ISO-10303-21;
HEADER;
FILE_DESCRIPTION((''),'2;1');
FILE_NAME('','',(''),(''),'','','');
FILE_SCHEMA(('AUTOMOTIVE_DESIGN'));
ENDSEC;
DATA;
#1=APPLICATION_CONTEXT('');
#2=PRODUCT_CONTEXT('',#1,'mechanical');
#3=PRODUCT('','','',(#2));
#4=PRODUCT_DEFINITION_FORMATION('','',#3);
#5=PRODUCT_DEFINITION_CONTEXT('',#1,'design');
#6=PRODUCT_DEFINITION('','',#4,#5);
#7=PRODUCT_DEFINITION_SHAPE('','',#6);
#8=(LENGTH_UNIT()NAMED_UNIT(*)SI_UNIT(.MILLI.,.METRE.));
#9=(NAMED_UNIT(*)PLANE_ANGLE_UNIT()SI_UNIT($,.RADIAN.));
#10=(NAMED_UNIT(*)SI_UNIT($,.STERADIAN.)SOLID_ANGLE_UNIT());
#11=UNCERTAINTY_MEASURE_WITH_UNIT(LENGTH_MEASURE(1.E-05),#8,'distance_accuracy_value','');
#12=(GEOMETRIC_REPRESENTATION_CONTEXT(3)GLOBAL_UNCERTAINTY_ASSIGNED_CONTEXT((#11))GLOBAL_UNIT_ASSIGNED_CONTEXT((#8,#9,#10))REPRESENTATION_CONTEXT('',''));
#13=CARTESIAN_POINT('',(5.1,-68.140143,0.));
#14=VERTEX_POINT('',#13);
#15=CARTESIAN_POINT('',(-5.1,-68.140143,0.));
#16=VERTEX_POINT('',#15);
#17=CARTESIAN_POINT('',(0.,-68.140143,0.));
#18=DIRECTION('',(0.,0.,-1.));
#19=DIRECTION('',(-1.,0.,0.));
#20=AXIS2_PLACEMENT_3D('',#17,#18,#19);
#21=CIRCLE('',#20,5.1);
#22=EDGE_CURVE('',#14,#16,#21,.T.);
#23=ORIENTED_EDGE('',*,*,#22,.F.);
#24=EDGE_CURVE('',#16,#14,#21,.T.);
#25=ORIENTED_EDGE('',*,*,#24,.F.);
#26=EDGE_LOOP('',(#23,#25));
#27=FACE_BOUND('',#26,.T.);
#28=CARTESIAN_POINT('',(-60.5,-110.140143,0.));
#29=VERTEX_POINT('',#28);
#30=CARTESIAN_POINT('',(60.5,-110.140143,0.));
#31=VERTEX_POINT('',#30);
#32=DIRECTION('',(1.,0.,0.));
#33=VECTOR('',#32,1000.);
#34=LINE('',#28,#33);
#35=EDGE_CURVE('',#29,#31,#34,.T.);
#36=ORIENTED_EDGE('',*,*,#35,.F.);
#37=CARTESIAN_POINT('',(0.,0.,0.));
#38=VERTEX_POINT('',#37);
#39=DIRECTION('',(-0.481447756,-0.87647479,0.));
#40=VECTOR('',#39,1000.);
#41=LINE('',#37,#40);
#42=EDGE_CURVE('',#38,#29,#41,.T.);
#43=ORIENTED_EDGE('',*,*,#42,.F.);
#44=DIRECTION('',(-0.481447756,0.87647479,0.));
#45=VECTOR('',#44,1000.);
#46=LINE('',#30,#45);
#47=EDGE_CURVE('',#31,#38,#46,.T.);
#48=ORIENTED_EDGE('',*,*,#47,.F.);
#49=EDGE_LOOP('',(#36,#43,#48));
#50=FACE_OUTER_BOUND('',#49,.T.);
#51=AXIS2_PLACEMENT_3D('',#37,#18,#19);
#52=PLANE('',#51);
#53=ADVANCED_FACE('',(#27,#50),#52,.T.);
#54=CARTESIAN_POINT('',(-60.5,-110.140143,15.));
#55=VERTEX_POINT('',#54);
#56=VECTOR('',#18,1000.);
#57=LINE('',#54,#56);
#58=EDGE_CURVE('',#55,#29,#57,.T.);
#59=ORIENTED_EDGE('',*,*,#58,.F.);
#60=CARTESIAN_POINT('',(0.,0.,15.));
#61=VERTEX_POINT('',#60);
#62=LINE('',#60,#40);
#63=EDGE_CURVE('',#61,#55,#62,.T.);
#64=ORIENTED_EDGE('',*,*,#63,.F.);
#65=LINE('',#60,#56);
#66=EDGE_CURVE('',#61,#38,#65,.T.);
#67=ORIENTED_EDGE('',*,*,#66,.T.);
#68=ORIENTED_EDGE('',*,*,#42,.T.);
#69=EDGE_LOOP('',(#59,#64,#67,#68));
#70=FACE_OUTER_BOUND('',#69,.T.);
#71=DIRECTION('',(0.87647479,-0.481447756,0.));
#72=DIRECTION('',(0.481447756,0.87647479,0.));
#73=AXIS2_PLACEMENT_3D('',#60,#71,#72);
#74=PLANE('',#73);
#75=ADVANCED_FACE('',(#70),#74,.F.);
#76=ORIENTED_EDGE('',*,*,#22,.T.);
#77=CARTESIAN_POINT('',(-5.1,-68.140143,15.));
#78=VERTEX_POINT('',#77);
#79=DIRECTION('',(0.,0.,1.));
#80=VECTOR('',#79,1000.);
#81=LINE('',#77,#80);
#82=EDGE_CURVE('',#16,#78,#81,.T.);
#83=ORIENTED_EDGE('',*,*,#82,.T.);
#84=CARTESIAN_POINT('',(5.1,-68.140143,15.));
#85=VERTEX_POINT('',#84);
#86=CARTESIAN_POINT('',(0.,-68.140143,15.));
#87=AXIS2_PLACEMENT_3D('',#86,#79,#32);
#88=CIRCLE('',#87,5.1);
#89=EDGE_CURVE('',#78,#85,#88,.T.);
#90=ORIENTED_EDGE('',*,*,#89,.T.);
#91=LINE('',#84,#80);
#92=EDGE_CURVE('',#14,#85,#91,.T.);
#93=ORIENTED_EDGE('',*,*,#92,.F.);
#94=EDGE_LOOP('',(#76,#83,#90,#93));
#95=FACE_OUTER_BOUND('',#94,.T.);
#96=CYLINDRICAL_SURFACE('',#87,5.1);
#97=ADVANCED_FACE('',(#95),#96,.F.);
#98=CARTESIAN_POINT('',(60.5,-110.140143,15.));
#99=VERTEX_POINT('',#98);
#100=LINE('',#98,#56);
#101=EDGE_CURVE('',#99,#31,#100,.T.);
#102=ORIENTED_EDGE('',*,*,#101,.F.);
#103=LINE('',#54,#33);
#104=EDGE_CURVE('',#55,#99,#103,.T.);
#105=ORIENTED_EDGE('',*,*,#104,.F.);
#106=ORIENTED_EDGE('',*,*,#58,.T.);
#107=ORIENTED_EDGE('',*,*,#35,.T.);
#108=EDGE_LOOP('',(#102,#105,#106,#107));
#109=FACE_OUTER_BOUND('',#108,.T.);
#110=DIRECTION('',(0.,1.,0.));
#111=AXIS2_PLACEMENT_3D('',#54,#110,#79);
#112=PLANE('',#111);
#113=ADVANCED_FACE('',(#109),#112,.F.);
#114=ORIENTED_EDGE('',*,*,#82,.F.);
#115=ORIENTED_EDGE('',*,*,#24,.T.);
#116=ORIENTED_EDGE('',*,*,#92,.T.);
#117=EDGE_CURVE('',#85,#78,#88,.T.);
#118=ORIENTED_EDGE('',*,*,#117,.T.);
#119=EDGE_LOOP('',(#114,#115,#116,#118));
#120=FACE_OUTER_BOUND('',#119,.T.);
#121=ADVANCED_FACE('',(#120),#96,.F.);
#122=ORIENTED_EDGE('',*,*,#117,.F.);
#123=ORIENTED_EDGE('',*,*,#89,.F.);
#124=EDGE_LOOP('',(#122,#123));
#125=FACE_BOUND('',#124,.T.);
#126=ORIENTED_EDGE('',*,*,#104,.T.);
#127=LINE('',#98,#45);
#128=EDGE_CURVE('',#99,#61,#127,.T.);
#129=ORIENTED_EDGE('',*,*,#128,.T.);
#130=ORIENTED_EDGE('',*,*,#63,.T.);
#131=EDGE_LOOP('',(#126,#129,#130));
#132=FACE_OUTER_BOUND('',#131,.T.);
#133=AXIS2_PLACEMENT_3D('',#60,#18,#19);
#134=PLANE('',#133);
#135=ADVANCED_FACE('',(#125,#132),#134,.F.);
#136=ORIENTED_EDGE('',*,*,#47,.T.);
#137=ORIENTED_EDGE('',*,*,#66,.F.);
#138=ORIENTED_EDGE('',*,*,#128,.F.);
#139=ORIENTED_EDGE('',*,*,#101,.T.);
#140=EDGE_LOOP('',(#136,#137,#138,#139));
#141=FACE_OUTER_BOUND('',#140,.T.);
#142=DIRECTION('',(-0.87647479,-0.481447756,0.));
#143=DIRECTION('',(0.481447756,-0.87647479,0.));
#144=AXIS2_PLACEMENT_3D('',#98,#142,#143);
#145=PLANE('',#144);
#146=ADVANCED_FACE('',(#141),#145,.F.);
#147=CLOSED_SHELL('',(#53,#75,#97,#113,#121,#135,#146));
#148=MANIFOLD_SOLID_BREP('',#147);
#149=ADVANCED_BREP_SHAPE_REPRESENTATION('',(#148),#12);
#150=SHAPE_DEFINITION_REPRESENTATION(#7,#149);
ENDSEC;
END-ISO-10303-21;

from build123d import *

# Parameters (mm, degrees)
SKETCH1_R              = 4.5
BOSS_EXTRUDE1_DEPTH    = 15
M12_TAPPED_HOLE1_D     = 10.2
M12_TAPPED_HOLE1_DEPTH = 29.25
M12_TAPPED_HOLE1_TIP   = 3.064389157


with BuildPart() as part:
    # Sketch1 → Boss-Extrude1 (new body)
    with BuildSketch(Plane.XY):
        Polygon((0, 0), (-60.5, -110.140143259), (60.5, -110.140143259), align=None)
        with Locations((0, -68.140143259)):
            Circle(SKETCH1_R, mode=Mode.SUBTRACT)
    extrude(amount=BOSS_EXTRUDE1_DEPTH)

    # M12 Tapped Hole1
    with Locations(Plane.XY.offset(15)):
        with Locations((0, -68.140143259)):
            Hole(M12_TAPPED_HOLE1_D / 2, depth=M12_TAPPED_HOLE1_DEPTH)
            with Locations((0, 0, -(M12_TAPPED_HOLE1_DEPTH + M12_TAPPED_HOLE1_TIP / 2))):  # 118° drill point
                Cone(0, M12_TAPPED_HOLE1_D / 2, M12_TAPPED_HOLE1_TIP, mode=Mode.SUBTRACT)


solid = part.part
